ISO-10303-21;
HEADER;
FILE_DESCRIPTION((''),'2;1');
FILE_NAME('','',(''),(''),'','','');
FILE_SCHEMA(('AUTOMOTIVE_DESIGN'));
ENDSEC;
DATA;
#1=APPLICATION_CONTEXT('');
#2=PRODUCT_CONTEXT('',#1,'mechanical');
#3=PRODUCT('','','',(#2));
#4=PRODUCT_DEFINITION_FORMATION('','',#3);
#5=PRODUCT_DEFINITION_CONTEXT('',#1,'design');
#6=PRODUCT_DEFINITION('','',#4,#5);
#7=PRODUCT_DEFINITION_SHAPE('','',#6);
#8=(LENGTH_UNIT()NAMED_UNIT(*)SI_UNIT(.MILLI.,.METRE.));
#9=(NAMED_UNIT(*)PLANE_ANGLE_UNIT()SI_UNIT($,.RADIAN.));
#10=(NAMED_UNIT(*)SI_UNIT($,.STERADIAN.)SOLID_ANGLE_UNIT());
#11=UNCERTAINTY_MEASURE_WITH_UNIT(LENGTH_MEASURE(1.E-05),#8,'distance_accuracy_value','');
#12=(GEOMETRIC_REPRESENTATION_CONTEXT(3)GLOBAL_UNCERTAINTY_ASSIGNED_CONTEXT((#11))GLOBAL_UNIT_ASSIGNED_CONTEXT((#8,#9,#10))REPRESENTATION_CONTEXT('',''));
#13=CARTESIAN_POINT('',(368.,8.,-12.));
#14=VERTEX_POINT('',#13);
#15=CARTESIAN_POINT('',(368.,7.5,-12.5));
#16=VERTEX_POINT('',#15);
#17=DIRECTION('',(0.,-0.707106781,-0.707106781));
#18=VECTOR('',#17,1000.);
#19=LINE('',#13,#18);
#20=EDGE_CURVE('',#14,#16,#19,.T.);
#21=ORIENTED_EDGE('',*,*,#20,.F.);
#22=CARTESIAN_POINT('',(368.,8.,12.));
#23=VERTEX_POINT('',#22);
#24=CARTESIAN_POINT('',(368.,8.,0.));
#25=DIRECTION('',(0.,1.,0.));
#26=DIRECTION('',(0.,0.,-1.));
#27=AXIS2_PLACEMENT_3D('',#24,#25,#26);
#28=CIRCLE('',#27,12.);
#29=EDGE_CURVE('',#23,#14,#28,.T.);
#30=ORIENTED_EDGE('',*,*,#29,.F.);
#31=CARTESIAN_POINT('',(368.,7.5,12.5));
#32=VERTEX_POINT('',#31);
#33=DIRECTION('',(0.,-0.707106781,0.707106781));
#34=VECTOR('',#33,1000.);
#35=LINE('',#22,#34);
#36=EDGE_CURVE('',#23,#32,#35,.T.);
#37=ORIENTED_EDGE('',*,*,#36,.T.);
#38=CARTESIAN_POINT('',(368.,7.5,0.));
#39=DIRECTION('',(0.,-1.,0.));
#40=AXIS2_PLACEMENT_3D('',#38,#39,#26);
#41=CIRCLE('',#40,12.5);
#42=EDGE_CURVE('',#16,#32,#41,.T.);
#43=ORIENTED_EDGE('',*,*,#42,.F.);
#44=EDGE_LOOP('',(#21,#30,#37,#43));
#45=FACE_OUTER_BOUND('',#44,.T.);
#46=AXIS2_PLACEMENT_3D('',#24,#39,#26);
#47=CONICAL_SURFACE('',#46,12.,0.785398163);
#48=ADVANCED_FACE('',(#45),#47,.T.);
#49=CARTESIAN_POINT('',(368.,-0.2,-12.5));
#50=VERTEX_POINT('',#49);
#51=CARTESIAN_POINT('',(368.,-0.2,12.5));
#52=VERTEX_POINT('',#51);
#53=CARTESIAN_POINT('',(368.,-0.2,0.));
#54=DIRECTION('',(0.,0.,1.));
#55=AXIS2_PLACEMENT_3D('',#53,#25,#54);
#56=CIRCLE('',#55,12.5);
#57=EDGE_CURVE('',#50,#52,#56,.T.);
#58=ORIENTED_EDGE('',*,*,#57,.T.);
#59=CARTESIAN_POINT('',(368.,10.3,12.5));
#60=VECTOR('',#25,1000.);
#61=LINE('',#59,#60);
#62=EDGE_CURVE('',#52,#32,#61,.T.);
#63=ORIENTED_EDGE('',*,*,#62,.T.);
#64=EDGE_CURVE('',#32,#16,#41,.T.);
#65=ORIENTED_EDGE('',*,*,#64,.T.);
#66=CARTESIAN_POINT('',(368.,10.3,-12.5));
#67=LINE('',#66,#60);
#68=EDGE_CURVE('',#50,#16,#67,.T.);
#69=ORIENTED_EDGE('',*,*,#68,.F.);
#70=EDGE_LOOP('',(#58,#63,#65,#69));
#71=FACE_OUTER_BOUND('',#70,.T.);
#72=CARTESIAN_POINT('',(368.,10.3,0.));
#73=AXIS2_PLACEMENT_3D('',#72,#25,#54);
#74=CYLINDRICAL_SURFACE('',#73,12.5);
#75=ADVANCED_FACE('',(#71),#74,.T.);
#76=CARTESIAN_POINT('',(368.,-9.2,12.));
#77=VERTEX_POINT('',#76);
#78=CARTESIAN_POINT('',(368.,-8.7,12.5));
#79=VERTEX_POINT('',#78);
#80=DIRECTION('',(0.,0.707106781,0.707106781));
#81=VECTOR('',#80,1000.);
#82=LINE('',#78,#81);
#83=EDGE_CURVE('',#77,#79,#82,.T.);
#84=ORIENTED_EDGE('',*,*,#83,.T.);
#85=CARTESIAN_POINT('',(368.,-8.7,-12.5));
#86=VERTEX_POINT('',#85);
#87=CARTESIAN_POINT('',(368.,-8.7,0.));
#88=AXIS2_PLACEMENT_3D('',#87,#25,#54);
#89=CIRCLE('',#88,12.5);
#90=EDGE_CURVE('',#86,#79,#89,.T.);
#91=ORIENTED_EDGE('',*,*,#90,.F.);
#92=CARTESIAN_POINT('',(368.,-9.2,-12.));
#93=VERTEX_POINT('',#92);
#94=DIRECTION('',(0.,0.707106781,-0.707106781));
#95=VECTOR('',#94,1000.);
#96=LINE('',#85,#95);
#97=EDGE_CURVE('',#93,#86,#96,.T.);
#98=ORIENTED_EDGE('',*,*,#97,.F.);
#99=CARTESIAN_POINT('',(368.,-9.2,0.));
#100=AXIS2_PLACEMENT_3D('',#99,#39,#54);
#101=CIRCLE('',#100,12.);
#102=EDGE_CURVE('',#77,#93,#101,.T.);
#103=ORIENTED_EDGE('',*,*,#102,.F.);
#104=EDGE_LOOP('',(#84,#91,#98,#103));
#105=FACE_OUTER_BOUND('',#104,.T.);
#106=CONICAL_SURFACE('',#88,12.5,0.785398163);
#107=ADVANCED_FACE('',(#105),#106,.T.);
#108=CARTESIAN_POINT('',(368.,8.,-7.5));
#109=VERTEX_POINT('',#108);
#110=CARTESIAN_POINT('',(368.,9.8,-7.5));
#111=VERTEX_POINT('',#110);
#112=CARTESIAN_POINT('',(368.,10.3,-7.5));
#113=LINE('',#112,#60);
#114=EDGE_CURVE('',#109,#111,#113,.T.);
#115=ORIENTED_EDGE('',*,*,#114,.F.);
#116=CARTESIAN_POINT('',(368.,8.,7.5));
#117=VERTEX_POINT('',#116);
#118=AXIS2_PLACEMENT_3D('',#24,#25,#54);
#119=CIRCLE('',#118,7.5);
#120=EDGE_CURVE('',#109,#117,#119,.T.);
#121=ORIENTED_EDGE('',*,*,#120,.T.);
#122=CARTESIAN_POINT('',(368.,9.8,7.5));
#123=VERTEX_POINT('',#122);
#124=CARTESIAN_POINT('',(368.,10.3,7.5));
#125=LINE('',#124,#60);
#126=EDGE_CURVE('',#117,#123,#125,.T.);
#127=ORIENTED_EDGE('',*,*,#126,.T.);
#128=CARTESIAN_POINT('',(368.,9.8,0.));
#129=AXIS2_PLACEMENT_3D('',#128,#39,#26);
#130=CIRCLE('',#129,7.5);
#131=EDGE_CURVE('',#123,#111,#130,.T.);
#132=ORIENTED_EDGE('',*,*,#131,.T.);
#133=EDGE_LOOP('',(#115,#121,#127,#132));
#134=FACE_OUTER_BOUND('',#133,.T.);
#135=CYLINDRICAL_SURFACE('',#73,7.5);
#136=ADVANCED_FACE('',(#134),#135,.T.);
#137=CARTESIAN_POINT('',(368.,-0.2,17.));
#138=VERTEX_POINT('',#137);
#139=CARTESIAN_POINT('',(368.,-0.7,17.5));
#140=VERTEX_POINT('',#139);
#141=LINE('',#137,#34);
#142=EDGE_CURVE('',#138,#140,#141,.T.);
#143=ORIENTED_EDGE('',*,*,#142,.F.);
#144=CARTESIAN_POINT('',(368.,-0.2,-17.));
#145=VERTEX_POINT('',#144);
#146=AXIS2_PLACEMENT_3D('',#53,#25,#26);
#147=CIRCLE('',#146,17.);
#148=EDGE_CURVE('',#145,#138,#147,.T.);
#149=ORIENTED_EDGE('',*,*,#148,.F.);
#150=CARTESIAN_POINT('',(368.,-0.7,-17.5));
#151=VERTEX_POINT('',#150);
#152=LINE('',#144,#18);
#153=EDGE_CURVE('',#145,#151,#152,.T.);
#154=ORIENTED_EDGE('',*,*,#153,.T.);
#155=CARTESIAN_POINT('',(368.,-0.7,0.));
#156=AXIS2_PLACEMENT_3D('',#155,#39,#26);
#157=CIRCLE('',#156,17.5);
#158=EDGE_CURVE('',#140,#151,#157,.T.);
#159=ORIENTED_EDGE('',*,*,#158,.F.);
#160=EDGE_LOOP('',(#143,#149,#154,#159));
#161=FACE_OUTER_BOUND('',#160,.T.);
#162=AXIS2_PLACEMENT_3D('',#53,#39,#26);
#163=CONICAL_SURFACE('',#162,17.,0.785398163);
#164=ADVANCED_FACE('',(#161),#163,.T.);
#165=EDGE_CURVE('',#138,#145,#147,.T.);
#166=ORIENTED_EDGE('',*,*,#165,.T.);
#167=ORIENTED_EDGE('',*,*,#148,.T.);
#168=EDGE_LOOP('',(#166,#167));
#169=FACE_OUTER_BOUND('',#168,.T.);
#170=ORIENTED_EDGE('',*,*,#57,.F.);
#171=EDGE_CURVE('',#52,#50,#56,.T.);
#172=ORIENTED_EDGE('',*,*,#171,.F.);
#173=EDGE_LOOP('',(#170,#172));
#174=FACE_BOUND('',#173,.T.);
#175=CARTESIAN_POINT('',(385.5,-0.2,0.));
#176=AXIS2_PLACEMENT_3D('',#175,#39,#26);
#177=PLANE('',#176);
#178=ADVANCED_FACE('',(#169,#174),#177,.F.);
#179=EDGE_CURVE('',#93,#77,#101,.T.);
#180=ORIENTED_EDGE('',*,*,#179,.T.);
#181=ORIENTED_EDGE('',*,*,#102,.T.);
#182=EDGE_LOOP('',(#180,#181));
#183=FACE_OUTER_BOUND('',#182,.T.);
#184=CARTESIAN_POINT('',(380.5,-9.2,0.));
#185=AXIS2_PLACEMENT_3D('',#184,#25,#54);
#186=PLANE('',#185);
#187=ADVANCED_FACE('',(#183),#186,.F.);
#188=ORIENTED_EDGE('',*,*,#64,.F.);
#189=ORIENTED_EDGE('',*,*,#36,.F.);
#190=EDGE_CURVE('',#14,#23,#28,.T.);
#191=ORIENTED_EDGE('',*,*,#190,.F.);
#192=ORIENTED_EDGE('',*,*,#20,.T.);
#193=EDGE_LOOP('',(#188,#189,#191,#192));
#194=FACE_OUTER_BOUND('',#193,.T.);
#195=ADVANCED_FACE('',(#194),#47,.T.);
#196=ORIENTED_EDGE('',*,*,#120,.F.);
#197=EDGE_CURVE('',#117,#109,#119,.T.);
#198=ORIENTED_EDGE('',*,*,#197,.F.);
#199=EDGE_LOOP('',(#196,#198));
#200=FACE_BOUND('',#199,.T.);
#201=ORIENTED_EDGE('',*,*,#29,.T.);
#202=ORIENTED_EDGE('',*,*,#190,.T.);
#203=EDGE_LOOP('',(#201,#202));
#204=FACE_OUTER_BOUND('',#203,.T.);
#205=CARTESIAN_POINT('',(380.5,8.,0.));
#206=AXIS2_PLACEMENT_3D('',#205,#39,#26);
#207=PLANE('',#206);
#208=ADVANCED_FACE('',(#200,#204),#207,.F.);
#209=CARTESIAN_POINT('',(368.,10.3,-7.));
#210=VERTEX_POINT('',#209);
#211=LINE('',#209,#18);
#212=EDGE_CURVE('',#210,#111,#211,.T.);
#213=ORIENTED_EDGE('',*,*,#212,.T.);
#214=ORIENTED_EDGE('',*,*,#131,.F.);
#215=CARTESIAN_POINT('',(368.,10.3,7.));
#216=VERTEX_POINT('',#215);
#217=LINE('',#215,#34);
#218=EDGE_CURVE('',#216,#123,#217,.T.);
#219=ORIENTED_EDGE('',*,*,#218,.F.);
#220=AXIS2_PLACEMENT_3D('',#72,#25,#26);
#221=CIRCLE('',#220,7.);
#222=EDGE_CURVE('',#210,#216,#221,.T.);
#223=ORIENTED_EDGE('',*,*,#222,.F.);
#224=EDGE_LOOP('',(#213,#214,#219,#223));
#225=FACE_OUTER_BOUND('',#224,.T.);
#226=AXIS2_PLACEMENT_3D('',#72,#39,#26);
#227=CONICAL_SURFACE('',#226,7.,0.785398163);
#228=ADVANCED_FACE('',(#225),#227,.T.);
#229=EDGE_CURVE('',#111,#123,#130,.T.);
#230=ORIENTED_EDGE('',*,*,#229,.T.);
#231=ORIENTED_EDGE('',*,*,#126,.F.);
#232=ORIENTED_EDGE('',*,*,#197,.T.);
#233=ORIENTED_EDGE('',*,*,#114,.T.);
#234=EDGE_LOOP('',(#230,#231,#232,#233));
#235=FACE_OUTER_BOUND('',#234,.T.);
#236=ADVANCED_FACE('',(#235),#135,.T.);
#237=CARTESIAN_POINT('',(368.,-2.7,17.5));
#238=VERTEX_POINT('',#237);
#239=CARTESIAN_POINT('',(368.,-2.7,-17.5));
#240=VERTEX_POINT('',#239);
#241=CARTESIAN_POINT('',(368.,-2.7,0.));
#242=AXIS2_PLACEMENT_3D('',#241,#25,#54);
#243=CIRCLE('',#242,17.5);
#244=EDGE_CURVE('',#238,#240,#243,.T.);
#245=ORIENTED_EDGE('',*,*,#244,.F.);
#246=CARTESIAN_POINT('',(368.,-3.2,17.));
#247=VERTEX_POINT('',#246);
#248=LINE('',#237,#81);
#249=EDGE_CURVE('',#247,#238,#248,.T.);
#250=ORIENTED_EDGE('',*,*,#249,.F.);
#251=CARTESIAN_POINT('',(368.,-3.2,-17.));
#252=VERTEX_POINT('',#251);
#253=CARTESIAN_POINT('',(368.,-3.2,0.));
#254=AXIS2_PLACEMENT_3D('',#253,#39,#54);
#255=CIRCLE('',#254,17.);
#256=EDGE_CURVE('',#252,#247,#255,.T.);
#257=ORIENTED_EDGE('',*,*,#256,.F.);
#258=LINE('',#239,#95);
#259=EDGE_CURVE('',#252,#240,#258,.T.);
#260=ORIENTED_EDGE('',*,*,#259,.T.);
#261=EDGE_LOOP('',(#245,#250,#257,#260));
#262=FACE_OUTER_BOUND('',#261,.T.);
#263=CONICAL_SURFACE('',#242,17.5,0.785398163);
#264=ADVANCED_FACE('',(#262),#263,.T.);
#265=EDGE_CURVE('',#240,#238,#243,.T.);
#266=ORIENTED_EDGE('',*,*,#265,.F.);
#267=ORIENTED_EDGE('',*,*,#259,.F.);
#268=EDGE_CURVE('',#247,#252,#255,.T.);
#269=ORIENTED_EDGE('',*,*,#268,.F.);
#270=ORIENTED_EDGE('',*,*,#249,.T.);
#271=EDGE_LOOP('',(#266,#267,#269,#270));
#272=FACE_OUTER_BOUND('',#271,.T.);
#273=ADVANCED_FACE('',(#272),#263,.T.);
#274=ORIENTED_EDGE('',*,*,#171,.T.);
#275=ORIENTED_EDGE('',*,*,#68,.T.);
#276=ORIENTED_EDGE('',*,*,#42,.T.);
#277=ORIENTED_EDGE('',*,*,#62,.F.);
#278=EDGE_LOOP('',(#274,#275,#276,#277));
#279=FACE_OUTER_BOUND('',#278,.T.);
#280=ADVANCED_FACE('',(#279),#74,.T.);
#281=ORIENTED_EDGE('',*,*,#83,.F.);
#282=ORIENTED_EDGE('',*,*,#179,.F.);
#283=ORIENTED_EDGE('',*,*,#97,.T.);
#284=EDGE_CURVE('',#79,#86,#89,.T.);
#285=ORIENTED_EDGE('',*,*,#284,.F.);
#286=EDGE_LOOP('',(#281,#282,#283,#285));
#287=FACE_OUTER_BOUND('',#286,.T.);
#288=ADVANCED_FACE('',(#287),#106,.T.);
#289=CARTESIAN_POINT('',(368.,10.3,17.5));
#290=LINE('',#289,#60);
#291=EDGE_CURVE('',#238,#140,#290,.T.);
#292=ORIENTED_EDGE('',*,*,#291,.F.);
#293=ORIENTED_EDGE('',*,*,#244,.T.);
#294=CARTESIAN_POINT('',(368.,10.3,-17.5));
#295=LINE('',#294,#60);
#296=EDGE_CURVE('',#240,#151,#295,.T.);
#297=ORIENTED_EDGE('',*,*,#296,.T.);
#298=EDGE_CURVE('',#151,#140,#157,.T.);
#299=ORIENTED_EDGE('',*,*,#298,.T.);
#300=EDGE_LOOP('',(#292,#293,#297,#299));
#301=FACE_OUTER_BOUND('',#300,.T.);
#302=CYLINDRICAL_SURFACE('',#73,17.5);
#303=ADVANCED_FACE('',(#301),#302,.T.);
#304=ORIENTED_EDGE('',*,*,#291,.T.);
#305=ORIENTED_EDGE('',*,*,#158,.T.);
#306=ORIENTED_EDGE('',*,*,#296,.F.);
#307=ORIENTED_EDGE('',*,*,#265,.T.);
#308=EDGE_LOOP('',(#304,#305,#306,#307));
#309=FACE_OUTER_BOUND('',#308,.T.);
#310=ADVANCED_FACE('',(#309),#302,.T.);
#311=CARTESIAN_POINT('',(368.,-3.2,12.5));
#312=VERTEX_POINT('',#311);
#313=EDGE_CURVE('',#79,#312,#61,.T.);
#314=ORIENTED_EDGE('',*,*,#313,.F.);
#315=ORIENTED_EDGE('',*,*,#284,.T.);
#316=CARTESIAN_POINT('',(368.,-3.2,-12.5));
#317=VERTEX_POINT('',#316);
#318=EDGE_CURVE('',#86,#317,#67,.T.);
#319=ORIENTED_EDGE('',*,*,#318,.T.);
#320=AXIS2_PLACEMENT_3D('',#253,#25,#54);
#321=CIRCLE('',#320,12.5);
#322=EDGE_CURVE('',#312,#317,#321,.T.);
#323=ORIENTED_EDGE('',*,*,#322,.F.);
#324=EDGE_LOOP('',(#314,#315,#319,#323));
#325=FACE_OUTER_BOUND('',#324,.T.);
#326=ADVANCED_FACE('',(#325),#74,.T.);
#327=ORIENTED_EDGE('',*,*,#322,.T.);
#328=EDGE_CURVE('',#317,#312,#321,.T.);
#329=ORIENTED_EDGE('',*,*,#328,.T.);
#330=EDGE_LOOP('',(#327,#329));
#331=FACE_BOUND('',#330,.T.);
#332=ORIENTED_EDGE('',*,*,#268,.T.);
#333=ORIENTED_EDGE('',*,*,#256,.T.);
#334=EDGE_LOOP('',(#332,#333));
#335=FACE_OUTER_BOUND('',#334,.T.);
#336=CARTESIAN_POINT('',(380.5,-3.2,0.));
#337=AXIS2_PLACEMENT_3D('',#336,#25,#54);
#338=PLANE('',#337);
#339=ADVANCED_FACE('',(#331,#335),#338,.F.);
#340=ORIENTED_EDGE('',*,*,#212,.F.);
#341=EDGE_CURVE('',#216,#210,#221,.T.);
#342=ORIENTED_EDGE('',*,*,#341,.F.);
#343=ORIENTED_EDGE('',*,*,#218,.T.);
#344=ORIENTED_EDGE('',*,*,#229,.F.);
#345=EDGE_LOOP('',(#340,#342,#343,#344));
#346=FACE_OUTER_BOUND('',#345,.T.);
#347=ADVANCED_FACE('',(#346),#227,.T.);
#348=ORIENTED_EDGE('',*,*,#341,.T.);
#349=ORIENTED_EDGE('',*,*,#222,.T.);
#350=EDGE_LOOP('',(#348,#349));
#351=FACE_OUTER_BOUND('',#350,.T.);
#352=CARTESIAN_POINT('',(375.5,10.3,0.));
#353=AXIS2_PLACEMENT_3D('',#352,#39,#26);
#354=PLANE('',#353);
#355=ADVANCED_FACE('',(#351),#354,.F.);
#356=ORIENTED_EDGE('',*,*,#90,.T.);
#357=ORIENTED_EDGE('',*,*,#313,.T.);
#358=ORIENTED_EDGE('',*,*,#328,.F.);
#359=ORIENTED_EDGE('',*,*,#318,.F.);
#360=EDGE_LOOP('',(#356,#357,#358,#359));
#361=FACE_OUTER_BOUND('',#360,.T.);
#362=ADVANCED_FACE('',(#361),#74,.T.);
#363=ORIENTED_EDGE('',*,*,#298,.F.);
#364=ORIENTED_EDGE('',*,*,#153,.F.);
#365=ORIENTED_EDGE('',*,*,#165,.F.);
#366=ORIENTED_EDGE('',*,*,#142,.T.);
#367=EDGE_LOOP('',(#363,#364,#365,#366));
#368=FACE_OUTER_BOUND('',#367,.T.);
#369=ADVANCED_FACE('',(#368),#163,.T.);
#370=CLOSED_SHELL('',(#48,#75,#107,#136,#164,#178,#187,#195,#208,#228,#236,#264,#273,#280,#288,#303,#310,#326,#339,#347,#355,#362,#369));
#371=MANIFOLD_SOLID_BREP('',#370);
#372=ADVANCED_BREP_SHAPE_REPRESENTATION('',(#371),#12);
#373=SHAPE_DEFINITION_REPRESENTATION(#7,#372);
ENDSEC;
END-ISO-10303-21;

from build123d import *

# Parameters (mm, degrees)
CHAMFER1_SIZE = 0.5


with BuildPart() as part:
    # Sketch1 → Revolve1 (revolve)
    with BuildSketch(Plane.XY, mode=Mode.PRIVATE) as revolve1_sk:
        Polygon((380.5, -9.2), (380.5, -3.2), (385.5, -3.2), (385.5, -0.2), (380.5, -0.2), (380.5, 8), (375.5, 8), (375.5, 10.3), (368, 10.3), (368, -9.2), align=None)
    revolve(revolve1_sk.sketch.rotate(Axis((368, 10.3, 0), (0, -1, 0)), 90), axis=Axis((368, 10.3, 0), (0, -1, 0)))

    # Chamfer1
    chamfer1_edges = [part.edges().sort_by_distance(p)[0] for p in [
        (368, -0.2, -17.5),
        (368, -3.2, -17.5),
        (368, -9.2, -12.5),
        (368, 10.3, -7.5),
        (368, 8, -12.5),
    ]]
    chamfer(chamfer1_edges, length=CHAMFER1_SIZE)


solid = part.part
